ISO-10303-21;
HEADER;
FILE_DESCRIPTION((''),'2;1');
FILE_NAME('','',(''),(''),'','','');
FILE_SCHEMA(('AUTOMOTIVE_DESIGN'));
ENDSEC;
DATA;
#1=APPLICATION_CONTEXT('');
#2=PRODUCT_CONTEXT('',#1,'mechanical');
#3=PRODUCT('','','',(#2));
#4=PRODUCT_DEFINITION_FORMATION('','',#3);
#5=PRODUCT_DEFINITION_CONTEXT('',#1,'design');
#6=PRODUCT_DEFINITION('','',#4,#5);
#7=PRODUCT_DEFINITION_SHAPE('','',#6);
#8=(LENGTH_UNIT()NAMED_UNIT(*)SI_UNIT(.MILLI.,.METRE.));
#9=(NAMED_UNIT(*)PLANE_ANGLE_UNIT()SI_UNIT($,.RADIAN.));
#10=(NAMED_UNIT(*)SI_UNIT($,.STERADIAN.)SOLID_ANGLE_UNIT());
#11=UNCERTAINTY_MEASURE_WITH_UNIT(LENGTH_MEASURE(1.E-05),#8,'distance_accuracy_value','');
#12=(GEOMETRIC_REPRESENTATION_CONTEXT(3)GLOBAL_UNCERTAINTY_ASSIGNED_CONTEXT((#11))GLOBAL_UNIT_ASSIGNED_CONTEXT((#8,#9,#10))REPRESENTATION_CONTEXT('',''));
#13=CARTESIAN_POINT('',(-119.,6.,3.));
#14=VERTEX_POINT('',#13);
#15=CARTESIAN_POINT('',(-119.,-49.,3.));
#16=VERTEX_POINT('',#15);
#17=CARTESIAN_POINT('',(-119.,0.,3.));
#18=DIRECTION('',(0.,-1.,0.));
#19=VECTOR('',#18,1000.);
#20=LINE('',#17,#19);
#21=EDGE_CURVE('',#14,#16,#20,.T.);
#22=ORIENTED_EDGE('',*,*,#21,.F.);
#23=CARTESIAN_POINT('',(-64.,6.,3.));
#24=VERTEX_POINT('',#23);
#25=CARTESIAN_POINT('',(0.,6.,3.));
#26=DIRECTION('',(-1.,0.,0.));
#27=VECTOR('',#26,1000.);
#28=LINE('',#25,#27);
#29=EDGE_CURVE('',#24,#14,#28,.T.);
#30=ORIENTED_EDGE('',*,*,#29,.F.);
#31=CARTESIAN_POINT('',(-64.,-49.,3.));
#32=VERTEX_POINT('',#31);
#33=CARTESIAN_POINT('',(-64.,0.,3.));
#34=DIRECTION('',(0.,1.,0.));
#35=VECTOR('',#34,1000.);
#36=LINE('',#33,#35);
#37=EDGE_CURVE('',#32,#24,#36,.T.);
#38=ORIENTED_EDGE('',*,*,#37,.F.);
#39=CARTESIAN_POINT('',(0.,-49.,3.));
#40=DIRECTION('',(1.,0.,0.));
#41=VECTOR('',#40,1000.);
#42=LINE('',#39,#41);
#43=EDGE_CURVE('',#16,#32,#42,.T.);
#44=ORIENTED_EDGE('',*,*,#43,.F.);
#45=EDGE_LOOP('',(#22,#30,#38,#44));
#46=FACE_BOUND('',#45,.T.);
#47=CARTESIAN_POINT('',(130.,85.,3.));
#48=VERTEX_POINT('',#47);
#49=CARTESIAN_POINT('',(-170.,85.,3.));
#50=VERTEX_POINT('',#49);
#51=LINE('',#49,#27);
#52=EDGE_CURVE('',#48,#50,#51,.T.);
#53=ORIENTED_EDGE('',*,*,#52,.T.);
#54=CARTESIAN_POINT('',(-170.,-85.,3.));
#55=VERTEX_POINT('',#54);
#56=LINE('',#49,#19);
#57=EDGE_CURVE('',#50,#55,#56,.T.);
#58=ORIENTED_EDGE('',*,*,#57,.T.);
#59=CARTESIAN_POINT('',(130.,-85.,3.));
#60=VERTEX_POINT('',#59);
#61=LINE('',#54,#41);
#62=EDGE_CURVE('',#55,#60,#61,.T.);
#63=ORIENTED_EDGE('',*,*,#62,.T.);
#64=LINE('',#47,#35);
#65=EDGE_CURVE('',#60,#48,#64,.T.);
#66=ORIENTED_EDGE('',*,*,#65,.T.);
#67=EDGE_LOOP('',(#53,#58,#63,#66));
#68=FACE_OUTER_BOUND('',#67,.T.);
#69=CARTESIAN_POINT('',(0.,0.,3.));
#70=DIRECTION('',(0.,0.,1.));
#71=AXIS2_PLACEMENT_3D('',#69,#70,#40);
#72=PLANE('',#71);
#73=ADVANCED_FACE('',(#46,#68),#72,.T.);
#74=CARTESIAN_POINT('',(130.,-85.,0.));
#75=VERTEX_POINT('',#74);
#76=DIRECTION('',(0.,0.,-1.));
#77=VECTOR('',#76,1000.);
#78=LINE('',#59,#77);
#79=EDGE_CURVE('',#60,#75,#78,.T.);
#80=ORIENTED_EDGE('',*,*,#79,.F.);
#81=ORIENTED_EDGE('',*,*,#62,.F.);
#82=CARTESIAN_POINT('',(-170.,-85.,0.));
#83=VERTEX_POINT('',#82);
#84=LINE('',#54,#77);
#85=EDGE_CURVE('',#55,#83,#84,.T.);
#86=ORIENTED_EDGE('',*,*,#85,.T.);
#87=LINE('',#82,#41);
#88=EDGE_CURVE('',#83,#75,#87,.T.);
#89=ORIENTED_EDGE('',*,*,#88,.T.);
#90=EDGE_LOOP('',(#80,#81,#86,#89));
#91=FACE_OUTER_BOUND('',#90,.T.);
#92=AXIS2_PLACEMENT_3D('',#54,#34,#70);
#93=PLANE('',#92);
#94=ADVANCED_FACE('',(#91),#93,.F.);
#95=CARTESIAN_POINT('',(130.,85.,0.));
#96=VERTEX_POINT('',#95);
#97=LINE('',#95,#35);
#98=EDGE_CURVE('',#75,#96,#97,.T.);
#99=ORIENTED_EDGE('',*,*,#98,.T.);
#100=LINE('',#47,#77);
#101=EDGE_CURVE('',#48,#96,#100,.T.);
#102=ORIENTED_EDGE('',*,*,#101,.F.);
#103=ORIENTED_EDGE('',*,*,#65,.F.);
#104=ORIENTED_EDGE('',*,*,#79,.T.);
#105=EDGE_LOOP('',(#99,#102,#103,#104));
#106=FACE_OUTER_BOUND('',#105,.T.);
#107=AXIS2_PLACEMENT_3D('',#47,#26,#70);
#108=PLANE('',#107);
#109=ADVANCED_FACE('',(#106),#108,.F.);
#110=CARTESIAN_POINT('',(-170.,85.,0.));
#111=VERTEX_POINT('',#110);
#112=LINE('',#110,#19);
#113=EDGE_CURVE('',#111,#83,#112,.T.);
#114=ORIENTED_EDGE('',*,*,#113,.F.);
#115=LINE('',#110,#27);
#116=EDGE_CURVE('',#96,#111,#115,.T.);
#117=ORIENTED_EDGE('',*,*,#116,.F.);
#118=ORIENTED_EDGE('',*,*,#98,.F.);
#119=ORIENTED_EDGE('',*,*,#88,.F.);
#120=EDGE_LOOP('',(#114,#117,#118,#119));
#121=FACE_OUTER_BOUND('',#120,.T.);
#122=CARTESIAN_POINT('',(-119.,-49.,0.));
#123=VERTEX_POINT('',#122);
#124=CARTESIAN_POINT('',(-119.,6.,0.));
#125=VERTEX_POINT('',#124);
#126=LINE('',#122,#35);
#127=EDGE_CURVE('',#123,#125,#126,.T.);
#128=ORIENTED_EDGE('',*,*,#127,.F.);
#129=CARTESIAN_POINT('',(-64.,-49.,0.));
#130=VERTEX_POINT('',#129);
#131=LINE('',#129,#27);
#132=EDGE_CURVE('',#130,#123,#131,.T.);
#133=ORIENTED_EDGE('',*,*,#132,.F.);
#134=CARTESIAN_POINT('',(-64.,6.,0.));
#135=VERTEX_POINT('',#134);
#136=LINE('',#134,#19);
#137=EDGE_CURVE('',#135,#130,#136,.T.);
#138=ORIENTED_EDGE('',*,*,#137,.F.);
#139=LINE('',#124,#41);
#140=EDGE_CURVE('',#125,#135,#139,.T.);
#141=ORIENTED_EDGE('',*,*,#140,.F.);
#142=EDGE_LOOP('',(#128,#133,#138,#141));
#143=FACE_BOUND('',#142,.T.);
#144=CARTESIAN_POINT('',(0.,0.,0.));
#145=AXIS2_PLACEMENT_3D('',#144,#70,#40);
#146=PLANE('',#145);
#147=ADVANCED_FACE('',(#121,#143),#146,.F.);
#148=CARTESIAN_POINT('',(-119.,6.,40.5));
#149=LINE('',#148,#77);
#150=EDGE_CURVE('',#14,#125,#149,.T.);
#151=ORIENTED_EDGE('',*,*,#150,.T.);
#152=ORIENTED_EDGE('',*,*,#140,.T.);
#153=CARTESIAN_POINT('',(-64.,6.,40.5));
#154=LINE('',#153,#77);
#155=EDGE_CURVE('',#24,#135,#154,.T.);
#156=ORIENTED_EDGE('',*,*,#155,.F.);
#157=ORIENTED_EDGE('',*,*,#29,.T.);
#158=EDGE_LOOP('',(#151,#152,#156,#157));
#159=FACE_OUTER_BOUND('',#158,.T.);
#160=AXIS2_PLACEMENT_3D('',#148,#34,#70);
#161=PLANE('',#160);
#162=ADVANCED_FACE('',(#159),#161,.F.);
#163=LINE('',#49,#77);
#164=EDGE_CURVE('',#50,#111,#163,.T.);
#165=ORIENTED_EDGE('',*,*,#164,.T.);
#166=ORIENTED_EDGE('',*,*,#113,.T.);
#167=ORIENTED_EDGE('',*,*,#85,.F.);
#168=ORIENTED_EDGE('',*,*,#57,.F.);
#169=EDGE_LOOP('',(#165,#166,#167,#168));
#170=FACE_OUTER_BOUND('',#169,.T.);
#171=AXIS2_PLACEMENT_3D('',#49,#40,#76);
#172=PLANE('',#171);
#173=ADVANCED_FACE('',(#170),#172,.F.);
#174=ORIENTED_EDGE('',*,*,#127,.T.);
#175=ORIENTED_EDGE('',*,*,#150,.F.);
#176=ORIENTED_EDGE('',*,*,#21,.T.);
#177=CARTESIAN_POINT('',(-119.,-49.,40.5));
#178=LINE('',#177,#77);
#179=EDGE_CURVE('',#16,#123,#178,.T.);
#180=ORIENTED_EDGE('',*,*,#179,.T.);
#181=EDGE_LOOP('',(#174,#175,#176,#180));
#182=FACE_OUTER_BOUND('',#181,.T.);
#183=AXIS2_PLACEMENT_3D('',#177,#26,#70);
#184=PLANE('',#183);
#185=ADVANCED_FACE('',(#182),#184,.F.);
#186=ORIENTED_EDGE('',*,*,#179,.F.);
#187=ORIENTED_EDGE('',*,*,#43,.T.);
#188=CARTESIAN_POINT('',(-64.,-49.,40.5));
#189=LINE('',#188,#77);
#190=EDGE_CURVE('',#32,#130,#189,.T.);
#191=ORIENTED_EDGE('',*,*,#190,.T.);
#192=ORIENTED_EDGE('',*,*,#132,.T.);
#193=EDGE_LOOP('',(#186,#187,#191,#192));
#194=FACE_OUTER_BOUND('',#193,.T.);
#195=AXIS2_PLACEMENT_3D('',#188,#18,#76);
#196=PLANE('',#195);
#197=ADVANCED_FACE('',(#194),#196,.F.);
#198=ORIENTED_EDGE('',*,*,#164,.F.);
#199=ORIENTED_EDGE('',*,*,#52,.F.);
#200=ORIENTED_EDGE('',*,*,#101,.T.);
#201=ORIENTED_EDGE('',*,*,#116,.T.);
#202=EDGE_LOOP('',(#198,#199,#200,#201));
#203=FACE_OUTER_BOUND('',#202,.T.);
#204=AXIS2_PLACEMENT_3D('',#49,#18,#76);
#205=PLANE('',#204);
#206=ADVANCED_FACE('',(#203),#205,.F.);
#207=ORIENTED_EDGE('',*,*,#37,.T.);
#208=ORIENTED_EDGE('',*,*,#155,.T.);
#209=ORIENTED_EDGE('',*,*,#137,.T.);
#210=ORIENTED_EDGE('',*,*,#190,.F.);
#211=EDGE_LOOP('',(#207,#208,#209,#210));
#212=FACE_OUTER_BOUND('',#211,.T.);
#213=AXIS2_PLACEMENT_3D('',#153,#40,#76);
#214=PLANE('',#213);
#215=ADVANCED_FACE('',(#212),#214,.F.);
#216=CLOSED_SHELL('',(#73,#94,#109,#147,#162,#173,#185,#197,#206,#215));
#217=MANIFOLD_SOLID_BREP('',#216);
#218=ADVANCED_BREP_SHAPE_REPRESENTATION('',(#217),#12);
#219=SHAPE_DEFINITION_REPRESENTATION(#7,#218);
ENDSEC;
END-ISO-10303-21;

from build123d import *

# Parameters (mm, degrees)
SKETCH1_W           = 300
SKETCH1_H           = 170
BOSS_EXTRUDE1_DEPTH = 3
SKETCH2_W           = 55
SKETCH2_H           = 55
CUT_EXTRUDE2_DEPTH  = 40.5


with BuildPart() as part:
    # Sketch1 → Boss-Extrude1 (new body)
    with BuildSketch(Plane.XY):
        with Locations((-20, 0)):
            Rectangle(SKETCH1_W, SKETCH1_H)
    extrude(amount=BOSS_EXTRUDE1_DEPTH)

    # Sketch2 → Cut-Extrude2 (cut)
    with BuildSketch(Plane(origin=(0, 0, 0), x_dir=(-1, 0, 0), z_dir=(0, 0, -1))):
        with Locations((91.5, -21.5)):
            Rectangle(SKETCH2_W, SKETCH2_H)
    extrude(amount=-CUT_EXTRUDE2_DEPTH, mode=Mode.SUBTRACT)


solid = part.part
